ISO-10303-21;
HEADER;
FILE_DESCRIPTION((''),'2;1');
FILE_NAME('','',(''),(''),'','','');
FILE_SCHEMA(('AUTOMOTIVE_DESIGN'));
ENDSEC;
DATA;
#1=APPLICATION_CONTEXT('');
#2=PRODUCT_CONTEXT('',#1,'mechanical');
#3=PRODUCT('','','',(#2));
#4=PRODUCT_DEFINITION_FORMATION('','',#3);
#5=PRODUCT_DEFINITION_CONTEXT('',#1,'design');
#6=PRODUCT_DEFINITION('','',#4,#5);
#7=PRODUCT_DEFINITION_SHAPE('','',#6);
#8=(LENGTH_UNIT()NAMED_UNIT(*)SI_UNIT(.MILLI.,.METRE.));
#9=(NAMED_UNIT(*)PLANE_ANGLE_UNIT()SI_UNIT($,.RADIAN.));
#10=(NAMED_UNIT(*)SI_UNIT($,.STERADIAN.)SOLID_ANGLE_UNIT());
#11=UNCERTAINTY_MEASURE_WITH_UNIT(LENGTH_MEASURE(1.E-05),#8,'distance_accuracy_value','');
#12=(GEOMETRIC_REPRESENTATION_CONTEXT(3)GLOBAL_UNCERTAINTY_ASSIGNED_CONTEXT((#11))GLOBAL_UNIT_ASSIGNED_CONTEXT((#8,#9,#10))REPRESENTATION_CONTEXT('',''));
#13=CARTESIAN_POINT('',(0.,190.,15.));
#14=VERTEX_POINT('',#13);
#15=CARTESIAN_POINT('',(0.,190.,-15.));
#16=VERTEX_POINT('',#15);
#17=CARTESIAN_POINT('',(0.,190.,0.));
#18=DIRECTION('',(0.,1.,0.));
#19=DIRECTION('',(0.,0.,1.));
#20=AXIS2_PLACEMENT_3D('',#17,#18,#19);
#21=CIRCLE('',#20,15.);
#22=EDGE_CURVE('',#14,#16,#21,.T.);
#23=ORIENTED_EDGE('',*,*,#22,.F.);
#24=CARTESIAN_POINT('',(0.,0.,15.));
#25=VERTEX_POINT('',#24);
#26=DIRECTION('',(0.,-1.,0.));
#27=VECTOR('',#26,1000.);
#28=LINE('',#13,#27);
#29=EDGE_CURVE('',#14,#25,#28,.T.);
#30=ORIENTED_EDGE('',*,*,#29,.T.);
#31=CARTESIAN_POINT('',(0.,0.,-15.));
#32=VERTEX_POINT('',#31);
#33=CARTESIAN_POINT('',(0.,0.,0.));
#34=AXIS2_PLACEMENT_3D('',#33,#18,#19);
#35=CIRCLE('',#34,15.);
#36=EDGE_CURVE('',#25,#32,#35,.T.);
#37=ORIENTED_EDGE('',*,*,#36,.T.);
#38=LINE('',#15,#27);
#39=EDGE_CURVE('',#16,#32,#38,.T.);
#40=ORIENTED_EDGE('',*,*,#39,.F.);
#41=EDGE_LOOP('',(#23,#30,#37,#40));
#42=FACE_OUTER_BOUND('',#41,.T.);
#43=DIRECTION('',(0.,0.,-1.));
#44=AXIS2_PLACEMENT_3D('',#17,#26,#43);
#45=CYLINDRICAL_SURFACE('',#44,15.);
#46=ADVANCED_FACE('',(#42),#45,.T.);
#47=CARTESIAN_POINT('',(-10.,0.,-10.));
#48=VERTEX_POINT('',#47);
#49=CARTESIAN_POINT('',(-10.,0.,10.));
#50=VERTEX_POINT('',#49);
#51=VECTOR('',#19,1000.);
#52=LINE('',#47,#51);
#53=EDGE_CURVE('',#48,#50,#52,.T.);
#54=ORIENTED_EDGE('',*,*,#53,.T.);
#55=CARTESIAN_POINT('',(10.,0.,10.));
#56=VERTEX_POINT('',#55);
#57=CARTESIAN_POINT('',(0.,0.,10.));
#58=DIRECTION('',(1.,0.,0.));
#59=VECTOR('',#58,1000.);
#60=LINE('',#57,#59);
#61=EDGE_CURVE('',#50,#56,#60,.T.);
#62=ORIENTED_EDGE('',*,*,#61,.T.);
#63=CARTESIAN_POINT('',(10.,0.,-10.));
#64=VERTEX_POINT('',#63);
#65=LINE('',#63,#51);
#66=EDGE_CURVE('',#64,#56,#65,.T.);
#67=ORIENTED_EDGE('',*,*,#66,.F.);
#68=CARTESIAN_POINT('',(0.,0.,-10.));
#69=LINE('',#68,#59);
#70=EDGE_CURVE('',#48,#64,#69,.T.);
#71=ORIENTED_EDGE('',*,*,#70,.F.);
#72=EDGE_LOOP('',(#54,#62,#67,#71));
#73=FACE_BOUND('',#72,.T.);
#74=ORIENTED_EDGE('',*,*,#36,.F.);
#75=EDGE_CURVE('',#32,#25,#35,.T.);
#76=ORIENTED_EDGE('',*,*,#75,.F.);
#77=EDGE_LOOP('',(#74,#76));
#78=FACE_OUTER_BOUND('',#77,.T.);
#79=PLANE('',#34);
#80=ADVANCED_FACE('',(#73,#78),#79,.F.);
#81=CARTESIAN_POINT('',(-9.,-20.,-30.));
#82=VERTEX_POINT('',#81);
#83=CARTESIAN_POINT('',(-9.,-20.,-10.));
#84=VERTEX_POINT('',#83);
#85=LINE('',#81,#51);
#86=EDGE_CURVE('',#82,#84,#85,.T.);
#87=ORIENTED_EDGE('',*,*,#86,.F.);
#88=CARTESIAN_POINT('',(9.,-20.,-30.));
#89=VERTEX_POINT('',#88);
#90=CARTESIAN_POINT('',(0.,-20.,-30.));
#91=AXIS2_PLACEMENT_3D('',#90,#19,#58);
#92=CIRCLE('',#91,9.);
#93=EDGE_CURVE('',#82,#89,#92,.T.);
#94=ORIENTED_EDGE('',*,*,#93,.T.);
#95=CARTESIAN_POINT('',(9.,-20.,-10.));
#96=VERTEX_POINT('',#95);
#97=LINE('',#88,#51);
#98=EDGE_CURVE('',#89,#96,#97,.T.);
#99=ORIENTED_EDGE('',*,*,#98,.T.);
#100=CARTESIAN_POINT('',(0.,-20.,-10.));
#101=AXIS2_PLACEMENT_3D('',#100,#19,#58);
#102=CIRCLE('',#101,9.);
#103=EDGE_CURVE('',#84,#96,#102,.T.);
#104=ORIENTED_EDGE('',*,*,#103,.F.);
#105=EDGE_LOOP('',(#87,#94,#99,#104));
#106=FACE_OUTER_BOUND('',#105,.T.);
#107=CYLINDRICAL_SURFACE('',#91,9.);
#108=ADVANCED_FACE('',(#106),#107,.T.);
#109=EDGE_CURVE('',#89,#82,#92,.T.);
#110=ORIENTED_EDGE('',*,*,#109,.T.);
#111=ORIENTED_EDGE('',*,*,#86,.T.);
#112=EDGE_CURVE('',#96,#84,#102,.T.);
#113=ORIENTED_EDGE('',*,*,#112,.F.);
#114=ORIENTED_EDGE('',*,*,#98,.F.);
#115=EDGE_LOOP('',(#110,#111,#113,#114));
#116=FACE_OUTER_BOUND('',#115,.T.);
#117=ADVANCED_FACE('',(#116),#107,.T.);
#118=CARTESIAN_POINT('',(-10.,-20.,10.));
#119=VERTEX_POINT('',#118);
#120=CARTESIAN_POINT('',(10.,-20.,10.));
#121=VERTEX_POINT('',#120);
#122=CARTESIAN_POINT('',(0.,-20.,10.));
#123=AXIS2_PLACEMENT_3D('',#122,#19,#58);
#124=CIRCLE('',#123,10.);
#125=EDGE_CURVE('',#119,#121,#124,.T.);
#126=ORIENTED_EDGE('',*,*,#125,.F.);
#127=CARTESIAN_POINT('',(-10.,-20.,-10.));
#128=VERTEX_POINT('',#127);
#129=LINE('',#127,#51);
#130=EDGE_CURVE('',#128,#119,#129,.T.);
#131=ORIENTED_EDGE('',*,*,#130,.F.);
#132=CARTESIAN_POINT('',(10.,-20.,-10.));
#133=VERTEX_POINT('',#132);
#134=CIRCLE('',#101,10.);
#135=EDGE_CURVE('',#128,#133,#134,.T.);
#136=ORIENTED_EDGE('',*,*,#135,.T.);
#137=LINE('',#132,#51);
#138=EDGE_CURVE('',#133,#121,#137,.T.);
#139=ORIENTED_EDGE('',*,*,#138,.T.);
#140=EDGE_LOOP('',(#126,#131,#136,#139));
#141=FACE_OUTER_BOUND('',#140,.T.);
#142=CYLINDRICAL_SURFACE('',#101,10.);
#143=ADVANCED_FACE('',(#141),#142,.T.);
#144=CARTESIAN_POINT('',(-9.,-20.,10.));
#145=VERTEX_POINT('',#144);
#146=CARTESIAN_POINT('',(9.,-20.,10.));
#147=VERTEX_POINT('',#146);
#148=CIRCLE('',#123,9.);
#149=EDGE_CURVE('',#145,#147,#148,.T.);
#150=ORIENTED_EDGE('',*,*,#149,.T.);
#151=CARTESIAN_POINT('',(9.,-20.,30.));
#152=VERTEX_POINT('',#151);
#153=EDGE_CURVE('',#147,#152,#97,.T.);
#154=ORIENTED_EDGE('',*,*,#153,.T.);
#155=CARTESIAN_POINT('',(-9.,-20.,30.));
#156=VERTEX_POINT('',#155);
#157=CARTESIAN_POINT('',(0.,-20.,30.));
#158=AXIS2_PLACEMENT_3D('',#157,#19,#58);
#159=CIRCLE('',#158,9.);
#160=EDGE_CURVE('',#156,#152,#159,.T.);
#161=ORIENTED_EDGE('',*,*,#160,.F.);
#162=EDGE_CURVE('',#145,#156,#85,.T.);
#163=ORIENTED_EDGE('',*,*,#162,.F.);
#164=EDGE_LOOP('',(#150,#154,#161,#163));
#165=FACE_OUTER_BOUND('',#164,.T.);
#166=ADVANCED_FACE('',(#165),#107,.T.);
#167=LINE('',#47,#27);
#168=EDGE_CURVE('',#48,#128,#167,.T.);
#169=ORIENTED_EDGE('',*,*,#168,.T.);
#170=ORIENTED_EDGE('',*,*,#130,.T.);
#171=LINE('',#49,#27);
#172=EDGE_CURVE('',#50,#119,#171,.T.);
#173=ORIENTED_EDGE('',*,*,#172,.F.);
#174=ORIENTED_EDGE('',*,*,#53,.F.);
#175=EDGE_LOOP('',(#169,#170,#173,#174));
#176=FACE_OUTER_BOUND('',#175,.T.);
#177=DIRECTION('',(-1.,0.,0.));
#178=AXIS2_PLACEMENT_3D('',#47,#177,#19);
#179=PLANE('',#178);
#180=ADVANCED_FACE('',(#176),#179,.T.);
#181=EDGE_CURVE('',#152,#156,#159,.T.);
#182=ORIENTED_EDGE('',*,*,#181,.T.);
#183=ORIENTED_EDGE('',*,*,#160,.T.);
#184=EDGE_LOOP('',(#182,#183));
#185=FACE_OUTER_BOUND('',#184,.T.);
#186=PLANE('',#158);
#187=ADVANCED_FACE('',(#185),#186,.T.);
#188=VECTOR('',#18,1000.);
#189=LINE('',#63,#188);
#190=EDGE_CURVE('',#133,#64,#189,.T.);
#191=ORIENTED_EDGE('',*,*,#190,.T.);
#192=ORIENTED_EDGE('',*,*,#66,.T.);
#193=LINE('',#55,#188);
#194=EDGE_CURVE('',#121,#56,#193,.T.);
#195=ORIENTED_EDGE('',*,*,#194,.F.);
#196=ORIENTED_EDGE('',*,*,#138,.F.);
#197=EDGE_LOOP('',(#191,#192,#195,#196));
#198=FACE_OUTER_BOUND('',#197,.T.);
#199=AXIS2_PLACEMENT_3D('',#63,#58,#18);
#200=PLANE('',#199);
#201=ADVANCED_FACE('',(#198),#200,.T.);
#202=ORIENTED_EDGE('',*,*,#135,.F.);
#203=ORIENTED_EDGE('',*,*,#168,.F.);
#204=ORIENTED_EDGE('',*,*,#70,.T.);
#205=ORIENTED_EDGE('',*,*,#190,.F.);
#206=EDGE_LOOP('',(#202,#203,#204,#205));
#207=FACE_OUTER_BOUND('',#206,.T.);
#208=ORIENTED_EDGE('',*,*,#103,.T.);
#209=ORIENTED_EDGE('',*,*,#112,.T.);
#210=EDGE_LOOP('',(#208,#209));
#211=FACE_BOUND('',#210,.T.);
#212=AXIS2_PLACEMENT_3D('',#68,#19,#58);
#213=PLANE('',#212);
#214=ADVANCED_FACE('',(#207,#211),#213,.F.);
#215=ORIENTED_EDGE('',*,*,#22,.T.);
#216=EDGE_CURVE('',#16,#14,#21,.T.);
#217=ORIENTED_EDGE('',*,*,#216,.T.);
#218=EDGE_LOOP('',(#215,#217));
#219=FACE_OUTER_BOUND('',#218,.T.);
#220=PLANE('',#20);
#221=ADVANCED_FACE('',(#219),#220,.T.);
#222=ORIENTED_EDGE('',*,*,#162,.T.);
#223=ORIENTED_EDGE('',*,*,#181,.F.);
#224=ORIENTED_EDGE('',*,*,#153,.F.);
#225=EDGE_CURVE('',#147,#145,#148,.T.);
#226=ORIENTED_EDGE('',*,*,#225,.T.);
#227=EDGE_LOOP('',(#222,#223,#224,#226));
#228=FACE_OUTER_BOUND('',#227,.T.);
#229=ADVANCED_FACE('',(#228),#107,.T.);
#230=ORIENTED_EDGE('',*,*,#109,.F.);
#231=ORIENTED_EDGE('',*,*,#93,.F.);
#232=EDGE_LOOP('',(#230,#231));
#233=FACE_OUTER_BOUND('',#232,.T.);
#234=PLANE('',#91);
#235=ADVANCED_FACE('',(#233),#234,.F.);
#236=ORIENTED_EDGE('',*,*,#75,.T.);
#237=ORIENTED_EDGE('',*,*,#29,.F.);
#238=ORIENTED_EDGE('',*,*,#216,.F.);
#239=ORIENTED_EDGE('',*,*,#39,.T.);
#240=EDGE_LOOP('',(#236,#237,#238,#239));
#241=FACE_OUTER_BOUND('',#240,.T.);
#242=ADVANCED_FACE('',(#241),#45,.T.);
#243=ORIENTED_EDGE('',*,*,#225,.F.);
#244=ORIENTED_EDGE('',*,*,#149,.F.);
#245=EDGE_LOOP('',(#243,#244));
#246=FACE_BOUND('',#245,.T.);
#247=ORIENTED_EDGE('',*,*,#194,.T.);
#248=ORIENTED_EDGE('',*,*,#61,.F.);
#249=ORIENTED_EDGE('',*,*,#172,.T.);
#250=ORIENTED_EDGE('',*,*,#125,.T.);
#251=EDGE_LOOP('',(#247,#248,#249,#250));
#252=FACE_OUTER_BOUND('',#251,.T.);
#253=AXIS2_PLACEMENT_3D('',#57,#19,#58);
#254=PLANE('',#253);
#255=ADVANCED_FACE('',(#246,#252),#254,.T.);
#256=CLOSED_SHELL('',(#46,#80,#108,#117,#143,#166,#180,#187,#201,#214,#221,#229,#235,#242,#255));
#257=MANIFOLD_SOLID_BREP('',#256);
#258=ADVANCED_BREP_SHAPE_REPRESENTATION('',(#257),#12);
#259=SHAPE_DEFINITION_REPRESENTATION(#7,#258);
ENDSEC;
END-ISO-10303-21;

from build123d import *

# Parameters (mm, degrees)
SKETCH_1_R           = 15
EXTRUDE_1_DEPTH      = 190
EXTRUDE_2_DEPTH      = 10
EXTRUDE_2_DEPTH_BACK = 10
EXTRUDE_3_DEPTH      = 20
EXTRUDE_3_DEPTH_BACK = 40
SKETCH_3_R           = 9


with BuildPart() as part:
    # 草图1 → 凸台-拉伸1 (new body)
    with BuildSketch(Plane(origin=(0, 0, 0), x_dir=(1, 0, 0), z_dir=(0, 1, 0))):
        with Locations(Location((0, 0, 0), (0, 0, 270))):
            Circle(SKETCH_1_R)
    extrude(amount=EXTRUDE_1_DEPTH)

    # 草图2 → 凸台-拉伸2 (add, two sides: drawn at the far end of the back side and taken through both)
    with BuildSketch(Plane.XY.offset(-EXTRUDE_2_DEPTH_BACK)):
        with BuildLine():
            Line((10, 0), (10, -20))
            ThreePointArc((10, -20), (0, -30), (-10, -20))
            Line((-10, -20), (-10, 0))
            ThreePointArc((-10, 0), (0, 10), (10, 0))
        make_face()
    extrude(amount=EXTRUDE_2_DEPTH + EXTRUDE_2_DEPTH_BACK)

    # 草图3 → 凸台-拉伸3 (add, two sides: drawn at the far end of the back side and taken through both)
    with BuildSketch(Plane.XY.offset(10).offset(-EXTRUDE_3_DEPTH_BACK)):
        with Locations((0, -20)):
            Circle(SKETCH_3_R)
    extrude(amount=EXTRUDE_3_DEPTH + EXTRUDE_3_DEPTH_BACK)


solid = part.part
